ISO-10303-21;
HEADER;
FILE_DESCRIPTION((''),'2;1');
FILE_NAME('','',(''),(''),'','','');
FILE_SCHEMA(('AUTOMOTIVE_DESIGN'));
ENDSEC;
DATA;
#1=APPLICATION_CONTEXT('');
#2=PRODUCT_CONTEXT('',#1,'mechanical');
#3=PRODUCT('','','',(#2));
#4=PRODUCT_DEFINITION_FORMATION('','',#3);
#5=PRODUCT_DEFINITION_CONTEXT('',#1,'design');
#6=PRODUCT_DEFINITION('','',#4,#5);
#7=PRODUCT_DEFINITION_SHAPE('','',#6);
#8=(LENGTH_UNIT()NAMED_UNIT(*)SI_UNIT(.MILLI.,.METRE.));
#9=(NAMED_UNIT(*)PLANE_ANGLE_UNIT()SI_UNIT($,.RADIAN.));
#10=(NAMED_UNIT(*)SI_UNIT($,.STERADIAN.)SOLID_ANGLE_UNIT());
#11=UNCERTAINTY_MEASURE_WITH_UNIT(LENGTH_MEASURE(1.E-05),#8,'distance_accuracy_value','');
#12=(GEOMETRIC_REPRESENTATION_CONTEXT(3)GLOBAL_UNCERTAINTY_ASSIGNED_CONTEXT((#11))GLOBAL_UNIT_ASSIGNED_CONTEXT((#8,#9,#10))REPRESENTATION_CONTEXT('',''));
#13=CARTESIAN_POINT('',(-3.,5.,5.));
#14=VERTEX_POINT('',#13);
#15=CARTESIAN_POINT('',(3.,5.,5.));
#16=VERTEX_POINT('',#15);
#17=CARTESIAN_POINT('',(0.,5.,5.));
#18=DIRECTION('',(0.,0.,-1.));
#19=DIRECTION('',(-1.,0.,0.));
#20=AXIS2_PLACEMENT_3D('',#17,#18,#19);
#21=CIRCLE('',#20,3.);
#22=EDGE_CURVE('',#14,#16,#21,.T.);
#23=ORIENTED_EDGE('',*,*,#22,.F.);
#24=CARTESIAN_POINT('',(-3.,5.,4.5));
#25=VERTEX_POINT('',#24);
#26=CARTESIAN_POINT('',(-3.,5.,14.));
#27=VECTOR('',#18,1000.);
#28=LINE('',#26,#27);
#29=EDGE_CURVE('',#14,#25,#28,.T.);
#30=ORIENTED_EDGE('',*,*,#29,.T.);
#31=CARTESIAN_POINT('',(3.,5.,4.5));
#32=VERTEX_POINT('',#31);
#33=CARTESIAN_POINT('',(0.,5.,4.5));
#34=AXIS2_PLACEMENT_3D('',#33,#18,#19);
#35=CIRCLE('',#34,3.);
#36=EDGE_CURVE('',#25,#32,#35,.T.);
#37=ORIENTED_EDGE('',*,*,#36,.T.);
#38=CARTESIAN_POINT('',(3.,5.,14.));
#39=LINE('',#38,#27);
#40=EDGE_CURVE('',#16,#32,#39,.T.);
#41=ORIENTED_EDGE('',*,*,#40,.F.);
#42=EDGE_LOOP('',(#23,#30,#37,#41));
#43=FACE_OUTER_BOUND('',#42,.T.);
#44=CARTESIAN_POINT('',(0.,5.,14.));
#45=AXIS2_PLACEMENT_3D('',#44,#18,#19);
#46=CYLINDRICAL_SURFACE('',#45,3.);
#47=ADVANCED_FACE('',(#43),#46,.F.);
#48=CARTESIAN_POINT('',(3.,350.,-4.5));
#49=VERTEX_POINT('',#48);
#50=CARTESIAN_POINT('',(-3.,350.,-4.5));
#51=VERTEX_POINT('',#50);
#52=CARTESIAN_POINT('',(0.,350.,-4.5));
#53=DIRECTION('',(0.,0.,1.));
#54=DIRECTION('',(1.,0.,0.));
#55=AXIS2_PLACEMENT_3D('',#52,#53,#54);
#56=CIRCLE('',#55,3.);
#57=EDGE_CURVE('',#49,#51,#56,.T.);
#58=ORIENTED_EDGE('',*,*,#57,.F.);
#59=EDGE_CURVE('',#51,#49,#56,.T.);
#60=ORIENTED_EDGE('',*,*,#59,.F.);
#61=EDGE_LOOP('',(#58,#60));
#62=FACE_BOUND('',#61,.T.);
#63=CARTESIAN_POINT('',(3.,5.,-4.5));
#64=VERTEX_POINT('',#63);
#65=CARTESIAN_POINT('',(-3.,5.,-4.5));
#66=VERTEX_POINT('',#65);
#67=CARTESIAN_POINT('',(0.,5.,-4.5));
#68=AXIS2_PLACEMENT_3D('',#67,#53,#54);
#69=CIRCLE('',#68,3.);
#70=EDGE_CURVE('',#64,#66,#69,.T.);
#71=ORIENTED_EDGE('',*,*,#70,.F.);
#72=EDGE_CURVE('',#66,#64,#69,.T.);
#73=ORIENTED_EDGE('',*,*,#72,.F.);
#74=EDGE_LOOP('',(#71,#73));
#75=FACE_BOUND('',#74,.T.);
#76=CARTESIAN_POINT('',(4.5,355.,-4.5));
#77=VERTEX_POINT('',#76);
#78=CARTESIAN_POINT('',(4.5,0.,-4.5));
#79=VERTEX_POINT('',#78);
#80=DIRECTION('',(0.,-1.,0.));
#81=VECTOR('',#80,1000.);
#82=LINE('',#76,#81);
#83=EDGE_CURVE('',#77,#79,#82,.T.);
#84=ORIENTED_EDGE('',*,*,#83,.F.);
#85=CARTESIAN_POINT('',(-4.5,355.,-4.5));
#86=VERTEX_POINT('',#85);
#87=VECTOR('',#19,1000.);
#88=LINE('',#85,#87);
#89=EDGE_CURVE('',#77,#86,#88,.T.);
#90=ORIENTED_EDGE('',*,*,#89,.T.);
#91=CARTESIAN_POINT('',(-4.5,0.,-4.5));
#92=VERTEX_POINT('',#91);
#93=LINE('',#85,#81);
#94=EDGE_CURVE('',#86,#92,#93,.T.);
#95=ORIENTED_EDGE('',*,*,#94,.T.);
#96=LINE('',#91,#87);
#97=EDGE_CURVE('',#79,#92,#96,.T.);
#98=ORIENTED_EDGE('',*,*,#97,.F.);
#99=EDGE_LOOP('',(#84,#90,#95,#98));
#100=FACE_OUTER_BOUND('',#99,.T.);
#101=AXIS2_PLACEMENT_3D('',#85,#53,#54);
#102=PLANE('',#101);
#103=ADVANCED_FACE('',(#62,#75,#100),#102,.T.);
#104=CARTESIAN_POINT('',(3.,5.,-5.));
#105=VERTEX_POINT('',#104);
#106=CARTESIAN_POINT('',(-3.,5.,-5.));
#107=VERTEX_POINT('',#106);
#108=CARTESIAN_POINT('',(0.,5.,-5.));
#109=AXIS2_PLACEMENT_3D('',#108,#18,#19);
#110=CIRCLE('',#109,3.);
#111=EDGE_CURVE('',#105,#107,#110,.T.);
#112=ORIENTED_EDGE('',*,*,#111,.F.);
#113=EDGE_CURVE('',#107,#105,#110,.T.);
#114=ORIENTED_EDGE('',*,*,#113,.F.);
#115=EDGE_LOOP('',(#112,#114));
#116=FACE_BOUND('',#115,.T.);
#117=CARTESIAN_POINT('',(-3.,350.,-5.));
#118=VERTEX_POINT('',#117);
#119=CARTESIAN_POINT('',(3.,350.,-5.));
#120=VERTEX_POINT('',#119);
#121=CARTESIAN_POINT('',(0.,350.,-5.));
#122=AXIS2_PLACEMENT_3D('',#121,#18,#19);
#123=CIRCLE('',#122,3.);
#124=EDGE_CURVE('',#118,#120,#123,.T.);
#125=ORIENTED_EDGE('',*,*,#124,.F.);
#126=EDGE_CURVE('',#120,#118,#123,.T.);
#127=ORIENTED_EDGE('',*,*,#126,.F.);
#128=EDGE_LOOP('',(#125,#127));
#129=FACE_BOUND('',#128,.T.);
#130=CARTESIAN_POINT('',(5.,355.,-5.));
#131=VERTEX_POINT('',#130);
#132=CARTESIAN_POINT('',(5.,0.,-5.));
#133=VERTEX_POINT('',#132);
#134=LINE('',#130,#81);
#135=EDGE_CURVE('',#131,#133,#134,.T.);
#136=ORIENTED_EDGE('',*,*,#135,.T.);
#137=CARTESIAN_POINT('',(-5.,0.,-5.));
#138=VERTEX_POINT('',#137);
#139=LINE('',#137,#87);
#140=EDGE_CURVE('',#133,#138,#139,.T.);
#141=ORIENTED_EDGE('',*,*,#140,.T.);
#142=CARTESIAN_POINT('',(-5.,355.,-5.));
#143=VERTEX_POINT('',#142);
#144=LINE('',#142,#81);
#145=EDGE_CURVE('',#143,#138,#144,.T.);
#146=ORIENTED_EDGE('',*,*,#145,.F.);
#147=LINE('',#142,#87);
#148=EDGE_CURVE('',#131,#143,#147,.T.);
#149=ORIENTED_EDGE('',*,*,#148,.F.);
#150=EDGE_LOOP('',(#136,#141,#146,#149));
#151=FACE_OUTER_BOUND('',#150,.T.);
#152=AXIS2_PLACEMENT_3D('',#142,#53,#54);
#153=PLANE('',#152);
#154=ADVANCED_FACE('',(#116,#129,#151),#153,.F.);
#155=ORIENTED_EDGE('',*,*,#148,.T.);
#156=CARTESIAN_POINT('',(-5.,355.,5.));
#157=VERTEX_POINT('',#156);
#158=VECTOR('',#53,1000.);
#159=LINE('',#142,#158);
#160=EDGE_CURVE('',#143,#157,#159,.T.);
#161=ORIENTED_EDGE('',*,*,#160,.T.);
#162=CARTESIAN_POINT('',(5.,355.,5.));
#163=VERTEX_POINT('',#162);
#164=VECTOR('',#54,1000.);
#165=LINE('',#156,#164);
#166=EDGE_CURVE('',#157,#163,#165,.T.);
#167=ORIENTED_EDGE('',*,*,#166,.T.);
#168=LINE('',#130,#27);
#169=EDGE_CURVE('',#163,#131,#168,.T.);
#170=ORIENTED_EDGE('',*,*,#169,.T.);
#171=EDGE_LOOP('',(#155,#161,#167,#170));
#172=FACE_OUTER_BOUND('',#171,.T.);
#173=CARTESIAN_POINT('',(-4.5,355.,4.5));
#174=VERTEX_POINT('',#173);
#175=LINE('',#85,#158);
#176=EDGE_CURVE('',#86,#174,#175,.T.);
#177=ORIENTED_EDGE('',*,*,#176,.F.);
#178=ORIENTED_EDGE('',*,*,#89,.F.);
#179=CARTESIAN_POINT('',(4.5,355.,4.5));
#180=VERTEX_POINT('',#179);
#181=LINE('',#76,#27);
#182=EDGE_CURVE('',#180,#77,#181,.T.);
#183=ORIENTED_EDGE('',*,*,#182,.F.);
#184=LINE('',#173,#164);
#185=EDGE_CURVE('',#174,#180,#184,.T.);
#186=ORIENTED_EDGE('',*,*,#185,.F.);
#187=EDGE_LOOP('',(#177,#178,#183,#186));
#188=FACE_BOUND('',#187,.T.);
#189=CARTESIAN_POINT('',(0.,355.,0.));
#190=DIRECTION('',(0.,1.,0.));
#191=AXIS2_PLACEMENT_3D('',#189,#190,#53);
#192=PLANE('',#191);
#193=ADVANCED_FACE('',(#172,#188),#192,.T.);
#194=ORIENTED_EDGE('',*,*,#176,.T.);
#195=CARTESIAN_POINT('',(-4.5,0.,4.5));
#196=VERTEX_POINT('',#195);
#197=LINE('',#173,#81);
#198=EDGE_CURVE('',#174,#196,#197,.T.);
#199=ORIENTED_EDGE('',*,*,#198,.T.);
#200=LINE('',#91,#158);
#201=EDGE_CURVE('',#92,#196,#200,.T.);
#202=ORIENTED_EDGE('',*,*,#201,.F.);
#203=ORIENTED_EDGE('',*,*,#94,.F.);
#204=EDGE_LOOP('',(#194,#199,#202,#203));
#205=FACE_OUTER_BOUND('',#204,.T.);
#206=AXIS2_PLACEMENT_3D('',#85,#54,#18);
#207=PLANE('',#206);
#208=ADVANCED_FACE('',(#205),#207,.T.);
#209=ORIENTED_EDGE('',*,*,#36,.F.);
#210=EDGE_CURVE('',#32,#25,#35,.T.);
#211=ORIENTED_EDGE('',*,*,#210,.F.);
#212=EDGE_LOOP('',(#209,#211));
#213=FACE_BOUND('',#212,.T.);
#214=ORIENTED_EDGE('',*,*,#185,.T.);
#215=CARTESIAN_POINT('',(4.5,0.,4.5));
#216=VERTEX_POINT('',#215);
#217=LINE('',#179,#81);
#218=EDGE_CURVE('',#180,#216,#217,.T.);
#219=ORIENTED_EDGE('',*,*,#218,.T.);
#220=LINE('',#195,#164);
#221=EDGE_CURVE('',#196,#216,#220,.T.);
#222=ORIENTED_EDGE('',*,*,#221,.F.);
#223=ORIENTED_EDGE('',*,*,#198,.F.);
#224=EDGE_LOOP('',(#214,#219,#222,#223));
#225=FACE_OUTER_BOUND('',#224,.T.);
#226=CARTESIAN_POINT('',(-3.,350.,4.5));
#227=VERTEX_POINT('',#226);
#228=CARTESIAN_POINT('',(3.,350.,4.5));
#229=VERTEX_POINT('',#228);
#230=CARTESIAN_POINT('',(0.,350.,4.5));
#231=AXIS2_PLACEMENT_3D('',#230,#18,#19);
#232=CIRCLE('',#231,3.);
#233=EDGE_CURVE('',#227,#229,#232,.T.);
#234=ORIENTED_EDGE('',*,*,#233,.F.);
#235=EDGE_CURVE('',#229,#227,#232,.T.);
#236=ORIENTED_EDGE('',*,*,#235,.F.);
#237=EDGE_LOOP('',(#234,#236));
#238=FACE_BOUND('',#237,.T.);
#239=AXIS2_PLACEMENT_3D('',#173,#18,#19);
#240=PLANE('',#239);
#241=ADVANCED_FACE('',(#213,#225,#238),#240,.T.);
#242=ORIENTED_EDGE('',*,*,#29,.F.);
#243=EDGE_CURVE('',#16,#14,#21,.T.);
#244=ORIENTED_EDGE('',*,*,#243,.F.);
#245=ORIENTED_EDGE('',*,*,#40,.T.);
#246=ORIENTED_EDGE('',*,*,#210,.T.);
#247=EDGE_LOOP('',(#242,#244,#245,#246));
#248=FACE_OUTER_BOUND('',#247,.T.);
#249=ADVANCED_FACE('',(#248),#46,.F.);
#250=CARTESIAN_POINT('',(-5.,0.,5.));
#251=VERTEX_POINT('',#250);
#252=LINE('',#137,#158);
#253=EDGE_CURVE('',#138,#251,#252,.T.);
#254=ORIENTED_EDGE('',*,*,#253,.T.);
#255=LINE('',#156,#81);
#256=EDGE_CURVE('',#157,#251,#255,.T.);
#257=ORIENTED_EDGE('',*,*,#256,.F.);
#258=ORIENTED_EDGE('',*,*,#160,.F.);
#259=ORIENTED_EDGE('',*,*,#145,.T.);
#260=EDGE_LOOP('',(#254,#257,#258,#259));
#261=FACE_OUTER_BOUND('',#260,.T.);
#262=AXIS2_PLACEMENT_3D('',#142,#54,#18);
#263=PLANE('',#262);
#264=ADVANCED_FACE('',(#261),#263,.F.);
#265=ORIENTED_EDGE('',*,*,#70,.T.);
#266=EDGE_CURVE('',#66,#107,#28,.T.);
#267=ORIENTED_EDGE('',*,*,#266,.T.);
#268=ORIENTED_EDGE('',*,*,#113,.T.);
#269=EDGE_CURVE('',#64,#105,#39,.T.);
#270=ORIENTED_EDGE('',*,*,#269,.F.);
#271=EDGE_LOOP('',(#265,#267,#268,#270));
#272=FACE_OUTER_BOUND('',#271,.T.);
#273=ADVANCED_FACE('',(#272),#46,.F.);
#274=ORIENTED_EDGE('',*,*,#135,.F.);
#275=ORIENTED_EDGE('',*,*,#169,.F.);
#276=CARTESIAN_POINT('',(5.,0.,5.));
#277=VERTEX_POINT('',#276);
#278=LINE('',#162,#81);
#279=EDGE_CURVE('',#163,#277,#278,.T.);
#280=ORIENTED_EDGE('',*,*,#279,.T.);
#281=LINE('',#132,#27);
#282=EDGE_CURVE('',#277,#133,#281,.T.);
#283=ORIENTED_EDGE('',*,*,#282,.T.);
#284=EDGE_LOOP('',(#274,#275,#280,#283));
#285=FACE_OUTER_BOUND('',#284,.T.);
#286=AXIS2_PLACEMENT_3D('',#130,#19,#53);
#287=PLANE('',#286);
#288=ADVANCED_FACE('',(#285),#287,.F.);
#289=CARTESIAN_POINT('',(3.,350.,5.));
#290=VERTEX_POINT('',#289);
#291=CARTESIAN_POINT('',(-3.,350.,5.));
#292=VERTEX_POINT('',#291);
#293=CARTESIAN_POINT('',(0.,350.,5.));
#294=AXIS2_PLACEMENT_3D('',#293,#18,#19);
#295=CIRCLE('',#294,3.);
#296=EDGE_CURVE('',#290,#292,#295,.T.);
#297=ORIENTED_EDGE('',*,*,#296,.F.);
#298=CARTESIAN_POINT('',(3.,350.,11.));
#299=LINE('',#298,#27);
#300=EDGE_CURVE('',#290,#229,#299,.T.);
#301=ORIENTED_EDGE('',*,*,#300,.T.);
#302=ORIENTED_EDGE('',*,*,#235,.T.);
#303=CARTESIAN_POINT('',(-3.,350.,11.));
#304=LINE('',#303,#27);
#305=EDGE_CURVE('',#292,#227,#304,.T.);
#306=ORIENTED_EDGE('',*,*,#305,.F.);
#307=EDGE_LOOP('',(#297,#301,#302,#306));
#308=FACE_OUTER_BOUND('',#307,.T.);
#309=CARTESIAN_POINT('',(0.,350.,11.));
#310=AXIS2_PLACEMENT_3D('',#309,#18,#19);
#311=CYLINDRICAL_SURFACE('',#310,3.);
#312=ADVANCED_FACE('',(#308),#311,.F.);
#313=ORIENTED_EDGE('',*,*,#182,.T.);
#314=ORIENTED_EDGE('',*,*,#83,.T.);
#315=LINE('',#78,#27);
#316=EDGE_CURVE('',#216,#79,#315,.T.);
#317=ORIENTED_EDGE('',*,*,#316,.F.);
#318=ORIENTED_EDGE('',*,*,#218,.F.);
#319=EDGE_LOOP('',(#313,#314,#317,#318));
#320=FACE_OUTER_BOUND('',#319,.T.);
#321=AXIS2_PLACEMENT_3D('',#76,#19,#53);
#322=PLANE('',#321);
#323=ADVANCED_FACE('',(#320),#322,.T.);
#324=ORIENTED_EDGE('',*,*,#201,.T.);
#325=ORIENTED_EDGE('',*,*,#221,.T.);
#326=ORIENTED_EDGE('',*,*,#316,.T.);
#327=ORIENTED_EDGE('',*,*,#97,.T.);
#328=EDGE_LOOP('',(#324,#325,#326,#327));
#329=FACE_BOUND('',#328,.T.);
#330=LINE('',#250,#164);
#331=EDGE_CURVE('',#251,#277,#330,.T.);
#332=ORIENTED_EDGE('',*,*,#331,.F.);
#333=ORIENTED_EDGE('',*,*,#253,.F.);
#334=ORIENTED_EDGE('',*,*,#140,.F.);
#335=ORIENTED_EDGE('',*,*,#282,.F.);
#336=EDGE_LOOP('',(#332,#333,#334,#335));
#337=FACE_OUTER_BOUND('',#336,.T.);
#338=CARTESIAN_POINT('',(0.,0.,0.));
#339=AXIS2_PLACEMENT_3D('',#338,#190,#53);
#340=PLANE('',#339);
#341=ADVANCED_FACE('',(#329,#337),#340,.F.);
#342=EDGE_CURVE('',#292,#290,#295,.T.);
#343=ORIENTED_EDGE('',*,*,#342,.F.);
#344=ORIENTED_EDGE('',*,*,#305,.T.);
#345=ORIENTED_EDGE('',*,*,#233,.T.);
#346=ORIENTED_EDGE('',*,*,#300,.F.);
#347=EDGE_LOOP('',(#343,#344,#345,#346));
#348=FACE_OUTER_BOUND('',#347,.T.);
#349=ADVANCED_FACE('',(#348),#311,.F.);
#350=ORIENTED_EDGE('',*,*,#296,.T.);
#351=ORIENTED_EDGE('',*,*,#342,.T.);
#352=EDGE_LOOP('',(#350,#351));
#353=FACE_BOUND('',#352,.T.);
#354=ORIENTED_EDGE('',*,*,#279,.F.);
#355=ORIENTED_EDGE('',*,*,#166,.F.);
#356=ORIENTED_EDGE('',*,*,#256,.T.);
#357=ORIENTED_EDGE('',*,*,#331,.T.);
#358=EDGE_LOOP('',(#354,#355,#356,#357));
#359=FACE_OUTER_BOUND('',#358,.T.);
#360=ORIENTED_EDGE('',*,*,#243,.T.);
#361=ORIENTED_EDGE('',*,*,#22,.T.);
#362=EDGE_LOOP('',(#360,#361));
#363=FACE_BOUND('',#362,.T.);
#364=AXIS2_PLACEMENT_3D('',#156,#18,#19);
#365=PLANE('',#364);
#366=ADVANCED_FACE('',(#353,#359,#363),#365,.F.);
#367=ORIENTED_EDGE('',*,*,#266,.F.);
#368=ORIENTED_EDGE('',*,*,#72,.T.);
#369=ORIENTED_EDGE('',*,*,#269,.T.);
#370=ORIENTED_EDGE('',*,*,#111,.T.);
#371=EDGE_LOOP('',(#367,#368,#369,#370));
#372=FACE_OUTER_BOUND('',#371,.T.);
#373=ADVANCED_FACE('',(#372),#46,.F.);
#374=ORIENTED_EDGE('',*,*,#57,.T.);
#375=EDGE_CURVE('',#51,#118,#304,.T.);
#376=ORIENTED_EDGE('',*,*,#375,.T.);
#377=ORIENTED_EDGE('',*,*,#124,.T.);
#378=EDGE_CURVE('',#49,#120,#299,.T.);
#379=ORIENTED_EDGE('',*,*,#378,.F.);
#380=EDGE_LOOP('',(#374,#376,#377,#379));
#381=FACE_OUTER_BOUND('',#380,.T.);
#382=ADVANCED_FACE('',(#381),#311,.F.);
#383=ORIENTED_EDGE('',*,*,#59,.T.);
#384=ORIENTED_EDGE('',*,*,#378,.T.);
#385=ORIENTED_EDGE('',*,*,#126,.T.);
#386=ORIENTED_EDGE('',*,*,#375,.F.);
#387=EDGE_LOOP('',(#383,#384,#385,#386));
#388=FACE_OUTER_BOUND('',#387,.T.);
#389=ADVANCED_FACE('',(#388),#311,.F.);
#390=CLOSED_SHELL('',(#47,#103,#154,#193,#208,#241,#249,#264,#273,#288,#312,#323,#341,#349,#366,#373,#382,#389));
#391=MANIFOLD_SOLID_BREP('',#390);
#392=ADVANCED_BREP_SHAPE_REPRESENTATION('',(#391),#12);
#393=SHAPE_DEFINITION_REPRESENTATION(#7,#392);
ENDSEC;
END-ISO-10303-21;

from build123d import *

# Parameters (mm, degrees)
SKETCH1_W           = 10
SKETCH1_H           = 10
SKETCH1_W_2         = 9
SKETCH1_H_2         = 9
BOSS_EXTRUDE1_DEPTH = 355
SKETCH2_R           = 3
CUT_EXTRUDE1_DEPTH  = 19
SKETCH3_R           = 3
CUT_EXTRUDE2_DEPTH  = 16


with BuildPart() as part:
    # Sketch1 → Boss-Extrude1 (new body)
    with BuildSketch(Plane(origin=(0, 0, 0), x_dir=(1, 0, 0), z_dir=(0, 1, 0))):
        Rectangle(SKETCH1_W, SKETCH1_H)
        Rectangle(SKETCH1_W_2, SKETCH1_H_2, mode=Mode.SUBTRACT)
    extrude(amount=BOSS_EXTRUDE1_DEPTH)

    # Sketch2 → Cut-Extrude1 (cut)
    with BuildSketch(Plane(origin=(0, 0, -5), x_dir=(-1, 0, 0), z_dir=(0, 0, -1))):
        with Locations((0, 5)):
            Circle(SKETCH2_R)
    extrude(amount=-CUT_EXTRUDE1_DEPTH, mode=Mode.SUBTRACT)

    # Sketch3 → Cut-Extrude2 (cut)
    with BuildSketch(Plane(origin=(0, 0, -5), x_dir=(-1, 0, 0), z_dir=(0, 0, -1))):
        with Locations((0, 350)):
            Circle(SKETCH3_R)
    extrude(amount=-CUT_EXTRUDE2_DEPTH, mode=Mode.SUBTRACT)


solid = part.part
